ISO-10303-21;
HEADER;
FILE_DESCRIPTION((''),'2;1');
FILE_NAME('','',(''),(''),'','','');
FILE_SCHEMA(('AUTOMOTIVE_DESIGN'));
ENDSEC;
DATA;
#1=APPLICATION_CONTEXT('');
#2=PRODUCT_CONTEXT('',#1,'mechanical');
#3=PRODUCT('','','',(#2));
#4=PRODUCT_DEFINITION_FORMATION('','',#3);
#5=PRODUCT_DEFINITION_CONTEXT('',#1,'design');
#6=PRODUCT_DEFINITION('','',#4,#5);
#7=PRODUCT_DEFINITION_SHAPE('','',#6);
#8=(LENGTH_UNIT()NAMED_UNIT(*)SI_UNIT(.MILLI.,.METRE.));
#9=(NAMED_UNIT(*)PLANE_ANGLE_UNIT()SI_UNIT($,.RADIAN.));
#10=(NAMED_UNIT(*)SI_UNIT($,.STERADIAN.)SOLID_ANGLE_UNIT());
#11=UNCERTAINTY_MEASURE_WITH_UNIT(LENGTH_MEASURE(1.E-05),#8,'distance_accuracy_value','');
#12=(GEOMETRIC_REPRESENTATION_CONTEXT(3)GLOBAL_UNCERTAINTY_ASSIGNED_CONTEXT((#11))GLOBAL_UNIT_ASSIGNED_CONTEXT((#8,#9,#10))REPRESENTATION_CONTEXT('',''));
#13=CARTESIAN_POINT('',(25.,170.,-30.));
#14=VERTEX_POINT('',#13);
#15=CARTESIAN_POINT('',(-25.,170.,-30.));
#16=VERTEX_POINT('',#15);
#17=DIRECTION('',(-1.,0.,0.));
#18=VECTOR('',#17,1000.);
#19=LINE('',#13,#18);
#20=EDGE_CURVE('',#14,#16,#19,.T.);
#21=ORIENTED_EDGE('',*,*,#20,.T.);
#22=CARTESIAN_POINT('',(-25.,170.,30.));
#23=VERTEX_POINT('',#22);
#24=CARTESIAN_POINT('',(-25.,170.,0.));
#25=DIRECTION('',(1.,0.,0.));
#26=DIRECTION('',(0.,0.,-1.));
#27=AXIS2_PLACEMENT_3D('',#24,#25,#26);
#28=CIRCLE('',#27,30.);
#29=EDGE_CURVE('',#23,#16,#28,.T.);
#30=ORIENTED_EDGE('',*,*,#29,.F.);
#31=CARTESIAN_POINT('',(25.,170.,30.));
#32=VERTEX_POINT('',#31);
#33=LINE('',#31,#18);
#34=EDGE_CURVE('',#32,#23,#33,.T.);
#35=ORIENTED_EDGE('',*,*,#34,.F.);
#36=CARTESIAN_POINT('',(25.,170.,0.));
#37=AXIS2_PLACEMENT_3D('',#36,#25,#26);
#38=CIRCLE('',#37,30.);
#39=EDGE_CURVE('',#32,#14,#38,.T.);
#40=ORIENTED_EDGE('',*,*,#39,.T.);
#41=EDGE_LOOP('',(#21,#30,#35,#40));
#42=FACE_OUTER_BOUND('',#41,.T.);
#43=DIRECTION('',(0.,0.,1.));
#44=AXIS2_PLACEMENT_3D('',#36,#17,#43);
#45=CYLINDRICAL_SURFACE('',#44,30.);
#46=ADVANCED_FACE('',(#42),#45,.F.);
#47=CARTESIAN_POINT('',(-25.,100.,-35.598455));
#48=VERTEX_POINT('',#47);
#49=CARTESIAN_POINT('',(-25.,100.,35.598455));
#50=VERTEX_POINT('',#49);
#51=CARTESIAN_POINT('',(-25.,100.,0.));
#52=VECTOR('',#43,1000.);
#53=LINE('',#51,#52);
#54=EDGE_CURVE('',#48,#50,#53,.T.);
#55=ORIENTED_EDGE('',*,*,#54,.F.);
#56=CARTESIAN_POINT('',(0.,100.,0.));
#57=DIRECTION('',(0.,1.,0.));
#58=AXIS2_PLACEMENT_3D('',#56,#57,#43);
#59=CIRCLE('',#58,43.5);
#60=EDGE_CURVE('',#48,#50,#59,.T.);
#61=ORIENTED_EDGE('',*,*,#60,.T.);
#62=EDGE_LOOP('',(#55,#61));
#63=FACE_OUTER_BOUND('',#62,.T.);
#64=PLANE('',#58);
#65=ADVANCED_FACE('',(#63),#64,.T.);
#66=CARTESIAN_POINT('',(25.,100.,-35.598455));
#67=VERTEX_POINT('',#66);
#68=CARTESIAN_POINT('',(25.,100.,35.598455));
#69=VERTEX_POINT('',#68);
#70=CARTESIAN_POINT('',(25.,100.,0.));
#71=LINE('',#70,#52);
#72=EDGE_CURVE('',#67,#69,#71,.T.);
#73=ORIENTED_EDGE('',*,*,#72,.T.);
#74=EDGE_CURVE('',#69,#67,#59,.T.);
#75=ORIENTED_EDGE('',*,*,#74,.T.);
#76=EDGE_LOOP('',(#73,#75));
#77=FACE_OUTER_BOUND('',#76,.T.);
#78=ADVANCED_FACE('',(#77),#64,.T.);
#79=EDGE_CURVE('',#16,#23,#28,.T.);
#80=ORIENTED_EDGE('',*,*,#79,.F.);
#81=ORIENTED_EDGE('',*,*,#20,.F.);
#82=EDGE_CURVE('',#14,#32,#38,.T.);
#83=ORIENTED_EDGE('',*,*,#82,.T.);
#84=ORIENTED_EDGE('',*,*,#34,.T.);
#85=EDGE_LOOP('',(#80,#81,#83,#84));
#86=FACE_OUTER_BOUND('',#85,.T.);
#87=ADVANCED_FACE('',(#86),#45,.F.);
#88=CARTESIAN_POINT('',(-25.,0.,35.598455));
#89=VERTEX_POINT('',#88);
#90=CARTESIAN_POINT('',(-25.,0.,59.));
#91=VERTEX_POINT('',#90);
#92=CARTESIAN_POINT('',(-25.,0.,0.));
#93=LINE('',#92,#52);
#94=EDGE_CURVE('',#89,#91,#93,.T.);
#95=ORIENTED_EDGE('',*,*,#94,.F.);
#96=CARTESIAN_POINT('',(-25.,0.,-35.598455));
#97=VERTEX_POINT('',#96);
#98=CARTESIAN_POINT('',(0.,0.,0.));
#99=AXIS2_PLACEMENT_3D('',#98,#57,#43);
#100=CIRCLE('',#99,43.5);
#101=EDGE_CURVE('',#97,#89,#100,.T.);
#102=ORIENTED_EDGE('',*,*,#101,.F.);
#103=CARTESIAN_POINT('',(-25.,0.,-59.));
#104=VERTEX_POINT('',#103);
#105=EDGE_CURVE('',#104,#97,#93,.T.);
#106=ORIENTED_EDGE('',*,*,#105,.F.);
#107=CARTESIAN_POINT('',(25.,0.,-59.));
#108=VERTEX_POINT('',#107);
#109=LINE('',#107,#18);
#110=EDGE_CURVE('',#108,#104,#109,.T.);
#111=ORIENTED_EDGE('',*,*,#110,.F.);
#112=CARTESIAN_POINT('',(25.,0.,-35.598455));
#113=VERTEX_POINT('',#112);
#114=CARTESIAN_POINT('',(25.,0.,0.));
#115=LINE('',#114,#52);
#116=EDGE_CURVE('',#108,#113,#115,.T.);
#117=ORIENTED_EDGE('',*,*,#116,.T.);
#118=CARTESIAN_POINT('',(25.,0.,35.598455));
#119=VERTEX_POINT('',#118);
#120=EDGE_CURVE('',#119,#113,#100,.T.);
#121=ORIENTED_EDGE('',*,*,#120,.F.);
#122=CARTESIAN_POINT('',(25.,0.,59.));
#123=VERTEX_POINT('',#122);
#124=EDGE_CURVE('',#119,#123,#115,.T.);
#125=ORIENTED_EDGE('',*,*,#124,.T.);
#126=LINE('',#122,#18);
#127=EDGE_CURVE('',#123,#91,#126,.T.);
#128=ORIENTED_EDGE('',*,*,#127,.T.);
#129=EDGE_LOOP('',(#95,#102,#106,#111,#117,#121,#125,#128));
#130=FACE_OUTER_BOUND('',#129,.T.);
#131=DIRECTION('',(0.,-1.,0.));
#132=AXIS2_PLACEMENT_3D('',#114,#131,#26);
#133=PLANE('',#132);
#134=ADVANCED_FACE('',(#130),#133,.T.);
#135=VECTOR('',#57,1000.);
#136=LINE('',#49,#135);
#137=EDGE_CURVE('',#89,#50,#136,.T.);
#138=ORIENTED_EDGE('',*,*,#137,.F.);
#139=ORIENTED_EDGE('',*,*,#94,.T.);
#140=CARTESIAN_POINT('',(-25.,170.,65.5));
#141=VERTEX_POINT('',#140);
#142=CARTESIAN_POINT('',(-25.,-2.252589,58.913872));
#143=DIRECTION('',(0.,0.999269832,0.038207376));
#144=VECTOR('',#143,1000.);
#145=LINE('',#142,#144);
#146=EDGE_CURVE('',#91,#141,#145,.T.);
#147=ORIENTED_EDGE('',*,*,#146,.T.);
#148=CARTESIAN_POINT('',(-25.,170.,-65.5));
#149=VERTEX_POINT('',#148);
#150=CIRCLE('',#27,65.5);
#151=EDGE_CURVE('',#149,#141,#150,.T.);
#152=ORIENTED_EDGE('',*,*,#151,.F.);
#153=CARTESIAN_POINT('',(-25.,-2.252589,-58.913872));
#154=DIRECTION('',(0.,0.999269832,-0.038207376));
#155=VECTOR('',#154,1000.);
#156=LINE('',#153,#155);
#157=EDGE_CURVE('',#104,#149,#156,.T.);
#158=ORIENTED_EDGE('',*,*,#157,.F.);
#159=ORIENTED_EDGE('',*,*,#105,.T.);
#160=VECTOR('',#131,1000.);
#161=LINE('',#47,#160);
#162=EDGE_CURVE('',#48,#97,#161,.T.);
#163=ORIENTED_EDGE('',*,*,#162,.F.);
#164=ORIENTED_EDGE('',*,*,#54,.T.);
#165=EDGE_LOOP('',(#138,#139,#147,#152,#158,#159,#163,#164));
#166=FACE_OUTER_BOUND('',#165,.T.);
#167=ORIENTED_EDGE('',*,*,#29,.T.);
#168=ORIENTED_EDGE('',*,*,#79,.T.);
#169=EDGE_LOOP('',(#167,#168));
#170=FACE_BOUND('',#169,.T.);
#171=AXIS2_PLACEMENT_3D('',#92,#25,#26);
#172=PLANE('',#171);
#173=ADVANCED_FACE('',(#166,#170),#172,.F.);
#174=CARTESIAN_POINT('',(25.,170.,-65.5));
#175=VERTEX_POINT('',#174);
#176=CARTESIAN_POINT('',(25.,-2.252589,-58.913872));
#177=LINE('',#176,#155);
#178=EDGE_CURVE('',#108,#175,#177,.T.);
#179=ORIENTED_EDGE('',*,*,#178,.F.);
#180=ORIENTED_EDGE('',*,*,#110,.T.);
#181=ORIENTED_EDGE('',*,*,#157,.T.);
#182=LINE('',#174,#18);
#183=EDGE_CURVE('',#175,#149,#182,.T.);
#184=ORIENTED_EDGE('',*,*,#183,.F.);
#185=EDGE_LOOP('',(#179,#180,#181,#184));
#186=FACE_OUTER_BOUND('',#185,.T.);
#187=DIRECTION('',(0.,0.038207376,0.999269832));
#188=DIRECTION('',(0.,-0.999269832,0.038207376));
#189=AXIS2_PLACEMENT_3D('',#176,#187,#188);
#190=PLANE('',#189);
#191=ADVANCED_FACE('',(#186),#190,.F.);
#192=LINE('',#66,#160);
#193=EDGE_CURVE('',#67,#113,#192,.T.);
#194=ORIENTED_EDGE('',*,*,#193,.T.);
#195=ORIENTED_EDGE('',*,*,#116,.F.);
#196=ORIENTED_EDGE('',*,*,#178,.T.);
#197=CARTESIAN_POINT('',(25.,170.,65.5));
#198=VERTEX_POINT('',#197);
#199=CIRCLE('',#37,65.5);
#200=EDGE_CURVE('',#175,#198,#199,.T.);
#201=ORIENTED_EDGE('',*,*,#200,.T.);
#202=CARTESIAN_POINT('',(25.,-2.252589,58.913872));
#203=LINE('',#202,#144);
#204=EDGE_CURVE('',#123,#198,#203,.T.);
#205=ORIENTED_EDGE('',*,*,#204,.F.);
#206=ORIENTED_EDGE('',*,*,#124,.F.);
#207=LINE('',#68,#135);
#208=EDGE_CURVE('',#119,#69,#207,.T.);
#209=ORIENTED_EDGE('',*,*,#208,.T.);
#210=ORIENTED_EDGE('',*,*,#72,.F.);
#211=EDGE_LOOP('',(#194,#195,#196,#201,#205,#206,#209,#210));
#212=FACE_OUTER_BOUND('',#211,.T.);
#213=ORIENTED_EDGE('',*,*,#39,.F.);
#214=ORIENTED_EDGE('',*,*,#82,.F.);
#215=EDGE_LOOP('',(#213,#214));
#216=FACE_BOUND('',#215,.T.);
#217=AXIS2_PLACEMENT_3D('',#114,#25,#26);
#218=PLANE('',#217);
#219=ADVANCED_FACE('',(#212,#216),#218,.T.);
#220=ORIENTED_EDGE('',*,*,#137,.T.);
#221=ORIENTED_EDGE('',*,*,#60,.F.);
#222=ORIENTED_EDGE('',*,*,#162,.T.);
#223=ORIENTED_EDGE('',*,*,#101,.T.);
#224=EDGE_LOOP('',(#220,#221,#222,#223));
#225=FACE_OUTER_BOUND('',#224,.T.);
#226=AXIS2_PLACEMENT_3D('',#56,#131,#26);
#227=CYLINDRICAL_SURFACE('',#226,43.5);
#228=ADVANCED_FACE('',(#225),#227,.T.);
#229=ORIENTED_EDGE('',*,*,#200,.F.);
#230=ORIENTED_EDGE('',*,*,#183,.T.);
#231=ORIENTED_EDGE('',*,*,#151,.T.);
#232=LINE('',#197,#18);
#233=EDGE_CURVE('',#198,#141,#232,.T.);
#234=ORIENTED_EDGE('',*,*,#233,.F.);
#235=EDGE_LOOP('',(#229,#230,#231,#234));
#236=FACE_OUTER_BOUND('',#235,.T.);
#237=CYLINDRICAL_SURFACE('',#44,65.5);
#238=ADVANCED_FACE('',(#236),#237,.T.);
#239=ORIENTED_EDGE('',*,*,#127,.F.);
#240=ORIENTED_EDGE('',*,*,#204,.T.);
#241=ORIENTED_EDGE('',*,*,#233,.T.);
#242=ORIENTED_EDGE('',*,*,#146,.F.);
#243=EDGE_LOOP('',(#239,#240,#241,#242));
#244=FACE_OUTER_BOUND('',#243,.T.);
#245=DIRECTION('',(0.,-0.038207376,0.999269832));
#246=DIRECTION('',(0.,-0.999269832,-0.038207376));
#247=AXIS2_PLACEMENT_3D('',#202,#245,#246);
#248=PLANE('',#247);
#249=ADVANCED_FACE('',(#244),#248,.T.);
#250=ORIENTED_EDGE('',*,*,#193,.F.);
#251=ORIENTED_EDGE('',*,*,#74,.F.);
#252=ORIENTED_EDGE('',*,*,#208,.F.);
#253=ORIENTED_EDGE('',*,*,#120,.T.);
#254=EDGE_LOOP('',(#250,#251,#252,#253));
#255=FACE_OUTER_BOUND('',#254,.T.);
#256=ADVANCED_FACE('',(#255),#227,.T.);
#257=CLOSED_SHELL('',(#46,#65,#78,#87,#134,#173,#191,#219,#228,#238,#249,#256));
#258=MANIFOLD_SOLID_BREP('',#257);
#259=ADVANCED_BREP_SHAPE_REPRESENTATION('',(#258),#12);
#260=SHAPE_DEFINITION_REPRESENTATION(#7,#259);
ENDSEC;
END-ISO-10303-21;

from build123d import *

# Parameters (mm, degrees)
SKETCH1_R           = 30
BOSS_EXTRUDE1_DEPTH = 25
SKETCH2_R           = 43.5
BOSS_EXTRUDE2_DEPTH = 100


with BuildPart() as part:
    # Sketch1 → Boss-Extrude1 (new, symmetric)
    with BuildSketch(Plane(origin=(0, 0, 0), x_dir=(0, 0, -1), z_dir=(1, 0, 0))):
        with BuildLine():
            Line((-65.5, 170), (-59, 0))
            Line((-59, 0), (59, 0))
            Line((59, 0), (65.5, 170))
            ThreePointArc((65.5, 170), (0, 235.5), (-65.5, 170))
        make_face()
        with Locations((0, 170)):
            Circle(SKETCH1_R, mode=Mode.SUBTRACT)
    extrude(amount=BOSS_EXTRUDE1_DEPTH, both=True)

    # Sketch2 → Boss-Extrude2 (add)
    with BuildSketch(Plane(origin=(0, 0, 0), x_dir=(1, 0, 0), z_dir=(0, 1, 0))):
        Circle(SKETCH2_R)
    extrude(amount=BOSS_EXTRUDE2_DEPTH)


solid = part.part
